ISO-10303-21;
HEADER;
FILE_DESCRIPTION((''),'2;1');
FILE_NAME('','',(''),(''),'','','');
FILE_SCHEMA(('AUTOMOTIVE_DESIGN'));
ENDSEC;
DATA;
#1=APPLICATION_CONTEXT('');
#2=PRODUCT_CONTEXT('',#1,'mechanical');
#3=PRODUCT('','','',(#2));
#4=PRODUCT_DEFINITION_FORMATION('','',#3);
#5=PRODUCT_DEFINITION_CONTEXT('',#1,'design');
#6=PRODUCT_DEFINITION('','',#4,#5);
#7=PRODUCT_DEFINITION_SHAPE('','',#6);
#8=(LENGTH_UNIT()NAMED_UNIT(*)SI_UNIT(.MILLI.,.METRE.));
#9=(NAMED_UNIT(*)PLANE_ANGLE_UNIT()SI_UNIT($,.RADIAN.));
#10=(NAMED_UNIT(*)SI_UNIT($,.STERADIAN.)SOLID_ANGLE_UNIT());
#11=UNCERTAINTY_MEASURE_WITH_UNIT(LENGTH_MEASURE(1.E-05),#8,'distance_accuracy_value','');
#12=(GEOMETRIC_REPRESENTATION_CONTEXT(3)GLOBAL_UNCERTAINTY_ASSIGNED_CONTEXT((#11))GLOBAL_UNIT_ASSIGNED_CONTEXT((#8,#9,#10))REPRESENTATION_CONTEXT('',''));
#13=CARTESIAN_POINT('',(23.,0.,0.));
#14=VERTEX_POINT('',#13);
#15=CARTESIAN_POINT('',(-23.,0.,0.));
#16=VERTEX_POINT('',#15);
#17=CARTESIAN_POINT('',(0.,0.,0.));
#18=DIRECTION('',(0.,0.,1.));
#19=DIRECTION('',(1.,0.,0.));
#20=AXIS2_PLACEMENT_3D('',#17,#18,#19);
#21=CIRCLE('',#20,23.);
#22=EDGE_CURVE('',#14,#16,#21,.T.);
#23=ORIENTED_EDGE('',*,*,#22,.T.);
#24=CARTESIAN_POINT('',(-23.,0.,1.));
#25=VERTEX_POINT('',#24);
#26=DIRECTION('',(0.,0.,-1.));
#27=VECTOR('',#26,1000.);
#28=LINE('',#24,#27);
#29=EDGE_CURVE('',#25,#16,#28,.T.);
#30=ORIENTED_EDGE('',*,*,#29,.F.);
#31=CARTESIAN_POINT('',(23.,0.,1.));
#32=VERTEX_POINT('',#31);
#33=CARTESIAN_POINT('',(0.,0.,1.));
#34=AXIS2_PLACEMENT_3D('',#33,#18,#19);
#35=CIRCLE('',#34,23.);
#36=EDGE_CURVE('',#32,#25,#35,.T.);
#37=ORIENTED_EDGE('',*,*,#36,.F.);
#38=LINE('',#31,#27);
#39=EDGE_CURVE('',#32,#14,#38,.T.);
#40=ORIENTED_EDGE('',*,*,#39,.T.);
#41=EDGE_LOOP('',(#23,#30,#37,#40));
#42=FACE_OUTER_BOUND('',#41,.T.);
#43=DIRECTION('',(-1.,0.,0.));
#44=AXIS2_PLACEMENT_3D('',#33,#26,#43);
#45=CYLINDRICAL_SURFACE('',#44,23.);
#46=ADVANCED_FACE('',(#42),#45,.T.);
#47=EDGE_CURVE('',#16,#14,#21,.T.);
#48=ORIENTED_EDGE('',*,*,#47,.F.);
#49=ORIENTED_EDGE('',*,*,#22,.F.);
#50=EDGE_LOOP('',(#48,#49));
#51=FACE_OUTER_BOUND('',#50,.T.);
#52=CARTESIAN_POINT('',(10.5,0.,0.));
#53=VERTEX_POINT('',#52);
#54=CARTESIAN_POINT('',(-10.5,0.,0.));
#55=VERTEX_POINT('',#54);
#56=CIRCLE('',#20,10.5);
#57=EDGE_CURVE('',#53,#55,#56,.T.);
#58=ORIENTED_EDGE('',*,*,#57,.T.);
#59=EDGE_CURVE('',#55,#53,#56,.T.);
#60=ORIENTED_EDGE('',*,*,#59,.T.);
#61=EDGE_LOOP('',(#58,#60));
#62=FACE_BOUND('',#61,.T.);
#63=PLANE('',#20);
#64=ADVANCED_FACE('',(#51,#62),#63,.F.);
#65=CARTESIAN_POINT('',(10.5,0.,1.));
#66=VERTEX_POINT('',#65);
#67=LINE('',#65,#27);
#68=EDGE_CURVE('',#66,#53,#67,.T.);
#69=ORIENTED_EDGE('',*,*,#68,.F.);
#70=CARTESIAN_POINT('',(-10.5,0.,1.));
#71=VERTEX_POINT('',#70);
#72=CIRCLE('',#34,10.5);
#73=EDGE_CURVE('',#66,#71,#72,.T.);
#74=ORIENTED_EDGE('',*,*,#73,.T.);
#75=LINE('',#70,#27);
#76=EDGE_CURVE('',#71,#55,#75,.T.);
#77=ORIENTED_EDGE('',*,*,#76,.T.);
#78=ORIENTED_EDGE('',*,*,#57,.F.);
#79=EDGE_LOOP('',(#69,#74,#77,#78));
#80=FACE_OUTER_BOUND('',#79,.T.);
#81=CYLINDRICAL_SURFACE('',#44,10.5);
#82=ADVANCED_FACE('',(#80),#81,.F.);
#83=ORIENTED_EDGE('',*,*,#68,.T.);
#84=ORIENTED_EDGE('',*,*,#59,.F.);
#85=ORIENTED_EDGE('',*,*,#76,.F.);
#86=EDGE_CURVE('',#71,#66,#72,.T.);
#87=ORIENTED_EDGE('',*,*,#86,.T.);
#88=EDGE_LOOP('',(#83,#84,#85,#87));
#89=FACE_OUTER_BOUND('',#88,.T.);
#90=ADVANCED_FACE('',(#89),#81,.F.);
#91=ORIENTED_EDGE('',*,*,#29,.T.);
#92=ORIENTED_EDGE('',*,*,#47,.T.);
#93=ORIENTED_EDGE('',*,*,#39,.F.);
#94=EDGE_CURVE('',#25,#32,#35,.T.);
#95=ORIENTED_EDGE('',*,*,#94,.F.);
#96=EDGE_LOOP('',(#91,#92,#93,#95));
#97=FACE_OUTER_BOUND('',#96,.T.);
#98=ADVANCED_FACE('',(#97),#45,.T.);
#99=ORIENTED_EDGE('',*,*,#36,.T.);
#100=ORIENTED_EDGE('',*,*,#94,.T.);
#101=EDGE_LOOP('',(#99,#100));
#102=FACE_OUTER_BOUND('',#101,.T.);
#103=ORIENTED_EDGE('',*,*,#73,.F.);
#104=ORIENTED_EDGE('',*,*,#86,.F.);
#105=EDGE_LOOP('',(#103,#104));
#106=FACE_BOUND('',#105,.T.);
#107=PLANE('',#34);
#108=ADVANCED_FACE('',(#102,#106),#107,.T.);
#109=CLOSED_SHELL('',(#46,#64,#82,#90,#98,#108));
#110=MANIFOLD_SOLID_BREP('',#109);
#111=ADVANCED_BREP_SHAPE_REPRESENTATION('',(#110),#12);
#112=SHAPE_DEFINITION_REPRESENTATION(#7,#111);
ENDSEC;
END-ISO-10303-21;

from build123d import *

# Parameters (mm, degrees)
SKETCH_1_R      = 23
SKETCH_1_R_2    = 10.5
EXTRUDE_1_DEPTH = 1


with BuildPart() as part:
    # 草图1 → 凸台-拉伸1 (new body)
    with BuildSketch(Plane.XY):
        Circle(SKETCH_1_R)
        Circle(SKETCH_1_R_2, mode=Mode.SUBTRACT)
    extrude(amount=EXTRUDE_1_DEPTH)


solid = part.part
